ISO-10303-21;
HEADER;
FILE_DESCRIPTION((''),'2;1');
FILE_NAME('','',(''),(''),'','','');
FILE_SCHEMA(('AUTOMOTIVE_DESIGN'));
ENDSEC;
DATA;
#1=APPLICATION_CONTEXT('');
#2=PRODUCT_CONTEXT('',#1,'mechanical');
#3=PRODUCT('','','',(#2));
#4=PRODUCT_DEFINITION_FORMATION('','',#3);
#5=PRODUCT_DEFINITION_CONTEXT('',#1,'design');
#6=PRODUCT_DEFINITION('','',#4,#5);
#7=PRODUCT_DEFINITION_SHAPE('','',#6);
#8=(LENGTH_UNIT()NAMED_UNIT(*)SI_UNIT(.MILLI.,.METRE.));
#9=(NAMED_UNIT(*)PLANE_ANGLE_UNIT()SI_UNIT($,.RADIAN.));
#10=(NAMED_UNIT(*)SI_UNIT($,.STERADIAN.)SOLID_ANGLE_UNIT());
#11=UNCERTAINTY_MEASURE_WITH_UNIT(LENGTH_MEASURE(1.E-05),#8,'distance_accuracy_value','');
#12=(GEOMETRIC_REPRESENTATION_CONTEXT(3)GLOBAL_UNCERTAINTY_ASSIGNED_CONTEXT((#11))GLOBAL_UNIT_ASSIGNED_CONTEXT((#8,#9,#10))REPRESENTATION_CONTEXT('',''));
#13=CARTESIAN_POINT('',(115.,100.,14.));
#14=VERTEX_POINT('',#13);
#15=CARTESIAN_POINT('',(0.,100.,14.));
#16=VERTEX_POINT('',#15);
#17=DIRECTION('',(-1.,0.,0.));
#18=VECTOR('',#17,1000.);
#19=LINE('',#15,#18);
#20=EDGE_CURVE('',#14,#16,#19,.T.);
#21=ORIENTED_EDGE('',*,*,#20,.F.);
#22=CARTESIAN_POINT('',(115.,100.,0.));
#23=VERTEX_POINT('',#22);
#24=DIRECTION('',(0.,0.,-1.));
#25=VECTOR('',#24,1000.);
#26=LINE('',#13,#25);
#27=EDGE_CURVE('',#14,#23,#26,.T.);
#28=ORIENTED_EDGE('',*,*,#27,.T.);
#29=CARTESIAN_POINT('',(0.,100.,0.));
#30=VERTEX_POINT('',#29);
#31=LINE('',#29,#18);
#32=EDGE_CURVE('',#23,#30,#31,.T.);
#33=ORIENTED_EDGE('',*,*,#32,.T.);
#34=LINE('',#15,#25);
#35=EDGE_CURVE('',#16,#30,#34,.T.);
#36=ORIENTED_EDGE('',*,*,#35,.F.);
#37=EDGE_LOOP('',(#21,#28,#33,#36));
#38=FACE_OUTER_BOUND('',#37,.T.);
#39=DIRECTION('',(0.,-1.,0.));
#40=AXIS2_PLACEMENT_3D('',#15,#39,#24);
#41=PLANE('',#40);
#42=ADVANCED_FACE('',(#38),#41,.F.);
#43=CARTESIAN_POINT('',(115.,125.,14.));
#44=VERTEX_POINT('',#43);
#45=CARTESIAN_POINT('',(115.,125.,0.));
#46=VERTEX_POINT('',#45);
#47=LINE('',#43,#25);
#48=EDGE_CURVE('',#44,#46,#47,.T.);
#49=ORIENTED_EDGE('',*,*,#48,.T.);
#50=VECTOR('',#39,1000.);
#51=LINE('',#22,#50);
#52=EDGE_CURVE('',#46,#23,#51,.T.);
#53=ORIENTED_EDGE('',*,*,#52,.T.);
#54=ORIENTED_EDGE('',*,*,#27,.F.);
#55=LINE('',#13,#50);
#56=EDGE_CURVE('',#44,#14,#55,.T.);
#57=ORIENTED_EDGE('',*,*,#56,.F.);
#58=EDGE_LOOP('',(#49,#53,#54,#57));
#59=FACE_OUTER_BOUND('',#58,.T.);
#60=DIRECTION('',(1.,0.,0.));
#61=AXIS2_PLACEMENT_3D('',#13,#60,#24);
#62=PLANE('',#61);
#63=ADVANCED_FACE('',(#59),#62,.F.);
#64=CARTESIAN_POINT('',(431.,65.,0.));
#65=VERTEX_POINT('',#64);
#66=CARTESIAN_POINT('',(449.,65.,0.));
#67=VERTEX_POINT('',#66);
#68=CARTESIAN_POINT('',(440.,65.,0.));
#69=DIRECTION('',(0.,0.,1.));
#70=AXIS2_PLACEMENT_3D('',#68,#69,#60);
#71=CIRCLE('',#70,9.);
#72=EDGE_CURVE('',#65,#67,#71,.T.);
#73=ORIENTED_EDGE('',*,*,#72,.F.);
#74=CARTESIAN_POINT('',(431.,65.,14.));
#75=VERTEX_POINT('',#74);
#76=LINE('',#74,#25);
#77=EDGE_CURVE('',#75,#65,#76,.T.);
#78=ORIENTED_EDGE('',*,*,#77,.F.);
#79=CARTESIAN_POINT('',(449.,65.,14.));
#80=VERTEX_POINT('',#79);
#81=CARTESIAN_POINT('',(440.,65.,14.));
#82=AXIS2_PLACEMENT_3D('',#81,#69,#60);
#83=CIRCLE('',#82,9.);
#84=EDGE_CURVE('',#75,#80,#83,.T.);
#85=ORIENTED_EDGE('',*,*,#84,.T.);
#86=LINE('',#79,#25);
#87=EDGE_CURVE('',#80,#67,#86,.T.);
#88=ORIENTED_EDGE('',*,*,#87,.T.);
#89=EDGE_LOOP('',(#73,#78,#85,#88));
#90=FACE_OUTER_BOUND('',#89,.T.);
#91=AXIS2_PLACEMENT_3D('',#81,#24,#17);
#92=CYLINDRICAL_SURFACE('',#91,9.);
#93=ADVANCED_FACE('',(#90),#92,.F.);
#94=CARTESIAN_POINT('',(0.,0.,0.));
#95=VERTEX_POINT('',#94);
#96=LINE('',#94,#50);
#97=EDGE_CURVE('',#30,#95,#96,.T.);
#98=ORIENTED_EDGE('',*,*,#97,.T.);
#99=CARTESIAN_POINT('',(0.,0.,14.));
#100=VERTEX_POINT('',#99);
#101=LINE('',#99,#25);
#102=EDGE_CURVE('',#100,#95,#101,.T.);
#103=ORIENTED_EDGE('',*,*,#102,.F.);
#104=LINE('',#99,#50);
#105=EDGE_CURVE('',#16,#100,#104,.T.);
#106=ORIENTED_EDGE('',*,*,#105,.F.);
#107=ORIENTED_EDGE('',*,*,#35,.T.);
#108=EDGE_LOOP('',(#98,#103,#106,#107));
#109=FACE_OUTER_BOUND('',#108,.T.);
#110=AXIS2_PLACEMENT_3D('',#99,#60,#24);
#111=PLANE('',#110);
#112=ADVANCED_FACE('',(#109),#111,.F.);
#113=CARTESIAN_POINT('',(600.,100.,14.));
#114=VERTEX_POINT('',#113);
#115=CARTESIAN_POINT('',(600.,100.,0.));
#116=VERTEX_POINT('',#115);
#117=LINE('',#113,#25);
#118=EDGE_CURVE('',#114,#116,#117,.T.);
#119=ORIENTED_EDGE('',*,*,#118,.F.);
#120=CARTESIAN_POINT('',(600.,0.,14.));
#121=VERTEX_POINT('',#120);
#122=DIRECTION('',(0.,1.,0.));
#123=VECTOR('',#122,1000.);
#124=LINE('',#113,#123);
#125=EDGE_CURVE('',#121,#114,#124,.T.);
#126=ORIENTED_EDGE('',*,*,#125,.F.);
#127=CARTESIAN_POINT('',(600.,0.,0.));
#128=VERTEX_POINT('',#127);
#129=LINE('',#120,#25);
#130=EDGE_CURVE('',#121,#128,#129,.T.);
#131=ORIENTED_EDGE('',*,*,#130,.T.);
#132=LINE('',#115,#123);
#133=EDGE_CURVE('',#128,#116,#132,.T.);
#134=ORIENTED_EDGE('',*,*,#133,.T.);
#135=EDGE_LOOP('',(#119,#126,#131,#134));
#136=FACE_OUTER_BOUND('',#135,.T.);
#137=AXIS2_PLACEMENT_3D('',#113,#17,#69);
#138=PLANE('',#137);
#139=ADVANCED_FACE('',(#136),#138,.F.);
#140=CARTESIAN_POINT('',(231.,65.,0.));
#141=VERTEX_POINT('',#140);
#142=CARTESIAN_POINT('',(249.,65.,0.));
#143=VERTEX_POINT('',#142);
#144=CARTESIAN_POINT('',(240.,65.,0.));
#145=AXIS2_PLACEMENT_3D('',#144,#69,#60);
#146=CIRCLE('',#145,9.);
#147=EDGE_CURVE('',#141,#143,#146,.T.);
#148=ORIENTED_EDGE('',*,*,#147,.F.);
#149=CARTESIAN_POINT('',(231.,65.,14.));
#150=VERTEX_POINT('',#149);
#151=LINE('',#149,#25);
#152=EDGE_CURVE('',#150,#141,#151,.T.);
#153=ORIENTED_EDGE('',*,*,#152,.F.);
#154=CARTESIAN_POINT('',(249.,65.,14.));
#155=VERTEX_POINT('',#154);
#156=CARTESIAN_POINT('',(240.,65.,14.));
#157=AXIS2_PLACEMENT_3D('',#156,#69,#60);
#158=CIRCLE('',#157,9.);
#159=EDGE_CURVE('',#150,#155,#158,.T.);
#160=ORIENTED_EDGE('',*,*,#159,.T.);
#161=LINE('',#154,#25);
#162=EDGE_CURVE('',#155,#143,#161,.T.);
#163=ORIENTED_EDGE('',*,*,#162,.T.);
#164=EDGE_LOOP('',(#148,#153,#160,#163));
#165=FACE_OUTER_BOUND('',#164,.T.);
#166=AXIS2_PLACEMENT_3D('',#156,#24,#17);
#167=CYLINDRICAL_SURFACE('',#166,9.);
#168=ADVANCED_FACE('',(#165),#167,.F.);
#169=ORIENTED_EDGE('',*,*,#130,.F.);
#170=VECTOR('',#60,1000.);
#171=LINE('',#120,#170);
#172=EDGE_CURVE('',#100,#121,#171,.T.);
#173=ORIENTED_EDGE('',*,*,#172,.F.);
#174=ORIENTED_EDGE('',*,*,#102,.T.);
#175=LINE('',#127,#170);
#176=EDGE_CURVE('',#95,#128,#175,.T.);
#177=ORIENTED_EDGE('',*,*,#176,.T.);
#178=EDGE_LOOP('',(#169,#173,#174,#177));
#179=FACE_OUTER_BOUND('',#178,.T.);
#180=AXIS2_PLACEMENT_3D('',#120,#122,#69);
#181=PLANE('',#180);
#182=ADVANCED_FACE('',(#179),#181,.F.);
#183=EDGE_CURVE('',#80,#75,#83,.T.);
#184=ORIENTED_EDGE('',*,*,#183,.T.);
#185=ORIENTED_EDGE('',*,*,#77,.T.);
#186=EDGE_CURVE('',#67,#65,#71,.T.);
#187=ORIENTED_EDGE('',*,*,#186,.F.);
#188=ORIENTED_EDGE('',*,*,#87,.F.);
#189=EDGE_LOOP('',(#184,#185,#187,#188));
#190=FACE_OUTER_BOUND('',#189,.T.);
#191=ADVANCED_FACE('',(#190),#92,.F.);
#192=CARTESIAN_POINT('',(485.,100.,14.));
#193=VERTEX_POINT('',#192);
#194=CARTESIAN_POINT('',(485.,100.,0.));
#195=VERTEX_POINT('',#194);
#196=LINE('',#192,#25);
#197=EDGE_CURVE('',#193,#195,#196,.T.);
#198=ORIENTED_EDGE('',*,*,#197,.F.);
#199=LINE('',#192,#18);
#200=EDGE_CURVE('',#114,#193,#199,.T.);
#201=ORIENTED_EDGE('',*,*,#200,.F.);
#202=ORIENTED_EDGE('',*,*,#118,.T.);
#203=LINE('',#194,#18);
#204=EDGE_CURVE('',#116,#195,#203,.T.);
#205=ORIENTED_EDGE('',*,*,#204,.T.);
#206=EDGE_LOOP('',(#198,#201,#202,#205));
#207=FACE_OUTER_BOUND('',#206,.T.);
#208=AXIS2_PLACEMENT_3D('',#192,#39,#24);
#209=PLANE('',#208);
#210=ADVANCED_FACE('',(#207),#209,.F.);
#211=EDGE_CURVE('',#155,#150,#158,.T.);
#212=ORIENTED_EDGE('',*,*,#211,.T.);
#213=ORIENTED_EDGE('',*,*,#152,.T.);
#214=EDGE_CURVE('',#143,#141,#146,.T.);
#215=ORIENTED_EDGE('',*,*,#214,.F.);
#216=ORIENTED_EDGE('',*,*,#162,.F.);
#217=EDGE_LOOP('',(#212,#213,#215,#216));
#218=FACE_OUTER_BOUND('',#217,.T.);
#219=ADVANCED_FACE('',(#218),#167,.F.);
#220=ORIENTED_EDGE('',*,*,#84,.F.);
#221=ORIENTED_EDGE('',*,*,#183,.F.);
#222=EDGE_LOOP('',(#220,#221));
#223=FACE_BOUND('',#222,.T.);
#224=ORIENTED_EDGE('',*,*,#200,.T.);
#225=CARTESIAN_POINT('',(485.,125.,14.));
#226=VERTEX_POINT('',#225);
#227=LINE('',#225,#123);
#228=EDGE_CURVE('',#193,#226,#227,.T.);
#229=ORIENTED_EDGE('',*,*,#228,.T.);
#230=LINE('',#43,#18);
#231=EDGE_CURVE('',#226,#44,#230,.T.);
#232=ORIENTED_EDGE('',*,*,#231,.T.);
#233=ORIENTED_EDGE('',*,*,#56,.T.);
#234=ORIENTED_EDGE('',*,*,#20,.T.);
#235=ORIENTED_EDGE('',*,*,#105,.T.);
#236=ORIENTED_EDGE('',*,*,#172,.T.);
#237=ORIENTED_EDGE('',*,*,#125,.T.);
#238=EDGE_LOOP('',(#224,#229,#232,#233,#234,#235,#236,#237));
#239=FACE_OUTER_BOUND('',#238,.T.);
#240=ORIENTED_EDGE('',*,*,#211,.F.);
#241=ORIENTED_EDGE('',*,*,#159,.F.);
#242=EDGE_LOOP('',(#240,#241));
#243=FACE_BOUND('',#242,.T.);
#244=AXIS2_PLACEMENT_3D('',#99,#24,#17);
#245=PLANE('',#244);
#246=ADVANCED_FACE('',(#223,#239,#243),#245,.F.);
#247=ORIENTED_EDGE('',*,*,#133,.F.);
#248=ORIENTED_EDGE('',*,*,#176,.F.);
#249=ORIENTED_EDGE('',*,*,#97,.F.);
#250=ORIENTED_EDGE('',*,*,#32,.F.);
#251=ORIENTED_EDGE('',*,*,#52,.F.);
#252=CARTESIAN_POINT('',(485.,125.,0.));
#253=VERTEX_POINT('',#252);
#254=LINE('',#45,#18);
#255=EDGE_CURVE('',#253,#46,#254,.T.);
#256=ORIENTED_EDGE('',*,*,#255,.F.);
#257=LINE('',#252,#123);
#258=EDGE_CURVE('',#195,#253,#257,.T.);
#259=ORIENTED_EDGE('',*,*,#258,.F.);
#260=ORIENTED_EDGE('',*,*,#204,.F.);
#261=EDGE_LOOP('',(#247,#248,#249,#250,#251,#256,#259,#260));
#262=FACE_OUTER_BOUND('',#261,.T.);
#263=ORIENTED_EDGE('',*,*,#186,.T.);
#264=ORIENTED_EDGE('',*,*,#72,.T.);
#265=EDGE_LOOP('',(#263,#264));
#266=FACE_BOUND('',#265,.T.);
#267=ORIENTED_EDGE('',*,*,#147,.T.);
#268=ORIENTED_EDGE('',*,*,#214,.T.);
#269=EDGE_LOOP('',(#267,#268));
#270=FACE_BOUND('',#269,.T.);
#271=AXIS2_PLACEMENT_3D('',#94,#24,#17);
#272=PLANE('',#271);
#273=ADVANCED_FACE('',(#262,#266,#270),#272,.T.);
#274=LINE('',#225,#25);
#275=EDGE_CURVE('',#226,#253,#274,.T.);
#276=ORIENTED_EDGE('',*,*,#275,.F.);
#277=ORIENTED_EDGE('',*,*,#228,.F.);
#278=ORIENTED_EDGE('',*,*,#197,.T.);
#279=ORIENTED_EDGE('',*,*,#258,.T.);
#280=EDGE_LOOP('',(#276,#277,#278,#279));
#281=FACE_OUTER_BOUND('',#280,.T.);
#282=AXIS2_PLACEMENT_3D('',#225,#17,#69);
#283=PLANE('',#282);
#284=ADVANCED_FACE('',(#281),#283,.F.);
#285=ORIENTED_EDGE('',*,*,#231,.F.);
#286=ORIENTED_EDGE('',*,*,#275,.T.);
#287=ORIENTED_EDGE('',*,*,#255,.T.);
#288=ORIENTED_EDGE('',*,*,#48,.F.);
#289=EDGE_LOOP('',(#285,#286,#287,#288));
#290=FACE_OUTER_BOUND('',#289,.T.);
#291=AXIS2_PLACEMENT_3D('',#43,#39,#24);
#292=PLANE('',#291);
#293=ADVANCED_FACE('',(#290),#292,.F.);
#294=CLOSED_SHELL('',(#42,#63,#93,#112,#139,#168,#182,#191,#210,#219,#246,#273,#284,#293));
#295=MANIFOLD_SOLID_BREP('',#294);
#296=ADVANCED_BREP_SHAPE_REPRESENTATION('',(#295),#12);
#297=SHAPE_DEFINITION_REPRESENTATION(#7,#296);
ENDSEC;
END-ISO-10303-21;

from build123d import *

# Parameters (mm, degrees)
SKETCH_1_R      = 9
EXTRUDE_1_DEPTH = 14


with BuildPart() as part:
    # 草图1 → 凸台-拉伸1 (new body)
    with BuildSketch(Plane.XY):
        Polygon((0, 0), (0, 100), (115, 100), (115, 125), (485, 125), (485, 100), (600, 100), (600, 0), align=None)
        with Locations((240, 65)):
            Circle(SKETCH_1_R, mode=Mode.SUBTRACT)
        with Locations((440, 65)):
            Circle(SKETCH_1_R, mode=Mode.SUBTRACT)
    extrude(amount=EXTRUDE_1_DEPTH)


solid = part.part
